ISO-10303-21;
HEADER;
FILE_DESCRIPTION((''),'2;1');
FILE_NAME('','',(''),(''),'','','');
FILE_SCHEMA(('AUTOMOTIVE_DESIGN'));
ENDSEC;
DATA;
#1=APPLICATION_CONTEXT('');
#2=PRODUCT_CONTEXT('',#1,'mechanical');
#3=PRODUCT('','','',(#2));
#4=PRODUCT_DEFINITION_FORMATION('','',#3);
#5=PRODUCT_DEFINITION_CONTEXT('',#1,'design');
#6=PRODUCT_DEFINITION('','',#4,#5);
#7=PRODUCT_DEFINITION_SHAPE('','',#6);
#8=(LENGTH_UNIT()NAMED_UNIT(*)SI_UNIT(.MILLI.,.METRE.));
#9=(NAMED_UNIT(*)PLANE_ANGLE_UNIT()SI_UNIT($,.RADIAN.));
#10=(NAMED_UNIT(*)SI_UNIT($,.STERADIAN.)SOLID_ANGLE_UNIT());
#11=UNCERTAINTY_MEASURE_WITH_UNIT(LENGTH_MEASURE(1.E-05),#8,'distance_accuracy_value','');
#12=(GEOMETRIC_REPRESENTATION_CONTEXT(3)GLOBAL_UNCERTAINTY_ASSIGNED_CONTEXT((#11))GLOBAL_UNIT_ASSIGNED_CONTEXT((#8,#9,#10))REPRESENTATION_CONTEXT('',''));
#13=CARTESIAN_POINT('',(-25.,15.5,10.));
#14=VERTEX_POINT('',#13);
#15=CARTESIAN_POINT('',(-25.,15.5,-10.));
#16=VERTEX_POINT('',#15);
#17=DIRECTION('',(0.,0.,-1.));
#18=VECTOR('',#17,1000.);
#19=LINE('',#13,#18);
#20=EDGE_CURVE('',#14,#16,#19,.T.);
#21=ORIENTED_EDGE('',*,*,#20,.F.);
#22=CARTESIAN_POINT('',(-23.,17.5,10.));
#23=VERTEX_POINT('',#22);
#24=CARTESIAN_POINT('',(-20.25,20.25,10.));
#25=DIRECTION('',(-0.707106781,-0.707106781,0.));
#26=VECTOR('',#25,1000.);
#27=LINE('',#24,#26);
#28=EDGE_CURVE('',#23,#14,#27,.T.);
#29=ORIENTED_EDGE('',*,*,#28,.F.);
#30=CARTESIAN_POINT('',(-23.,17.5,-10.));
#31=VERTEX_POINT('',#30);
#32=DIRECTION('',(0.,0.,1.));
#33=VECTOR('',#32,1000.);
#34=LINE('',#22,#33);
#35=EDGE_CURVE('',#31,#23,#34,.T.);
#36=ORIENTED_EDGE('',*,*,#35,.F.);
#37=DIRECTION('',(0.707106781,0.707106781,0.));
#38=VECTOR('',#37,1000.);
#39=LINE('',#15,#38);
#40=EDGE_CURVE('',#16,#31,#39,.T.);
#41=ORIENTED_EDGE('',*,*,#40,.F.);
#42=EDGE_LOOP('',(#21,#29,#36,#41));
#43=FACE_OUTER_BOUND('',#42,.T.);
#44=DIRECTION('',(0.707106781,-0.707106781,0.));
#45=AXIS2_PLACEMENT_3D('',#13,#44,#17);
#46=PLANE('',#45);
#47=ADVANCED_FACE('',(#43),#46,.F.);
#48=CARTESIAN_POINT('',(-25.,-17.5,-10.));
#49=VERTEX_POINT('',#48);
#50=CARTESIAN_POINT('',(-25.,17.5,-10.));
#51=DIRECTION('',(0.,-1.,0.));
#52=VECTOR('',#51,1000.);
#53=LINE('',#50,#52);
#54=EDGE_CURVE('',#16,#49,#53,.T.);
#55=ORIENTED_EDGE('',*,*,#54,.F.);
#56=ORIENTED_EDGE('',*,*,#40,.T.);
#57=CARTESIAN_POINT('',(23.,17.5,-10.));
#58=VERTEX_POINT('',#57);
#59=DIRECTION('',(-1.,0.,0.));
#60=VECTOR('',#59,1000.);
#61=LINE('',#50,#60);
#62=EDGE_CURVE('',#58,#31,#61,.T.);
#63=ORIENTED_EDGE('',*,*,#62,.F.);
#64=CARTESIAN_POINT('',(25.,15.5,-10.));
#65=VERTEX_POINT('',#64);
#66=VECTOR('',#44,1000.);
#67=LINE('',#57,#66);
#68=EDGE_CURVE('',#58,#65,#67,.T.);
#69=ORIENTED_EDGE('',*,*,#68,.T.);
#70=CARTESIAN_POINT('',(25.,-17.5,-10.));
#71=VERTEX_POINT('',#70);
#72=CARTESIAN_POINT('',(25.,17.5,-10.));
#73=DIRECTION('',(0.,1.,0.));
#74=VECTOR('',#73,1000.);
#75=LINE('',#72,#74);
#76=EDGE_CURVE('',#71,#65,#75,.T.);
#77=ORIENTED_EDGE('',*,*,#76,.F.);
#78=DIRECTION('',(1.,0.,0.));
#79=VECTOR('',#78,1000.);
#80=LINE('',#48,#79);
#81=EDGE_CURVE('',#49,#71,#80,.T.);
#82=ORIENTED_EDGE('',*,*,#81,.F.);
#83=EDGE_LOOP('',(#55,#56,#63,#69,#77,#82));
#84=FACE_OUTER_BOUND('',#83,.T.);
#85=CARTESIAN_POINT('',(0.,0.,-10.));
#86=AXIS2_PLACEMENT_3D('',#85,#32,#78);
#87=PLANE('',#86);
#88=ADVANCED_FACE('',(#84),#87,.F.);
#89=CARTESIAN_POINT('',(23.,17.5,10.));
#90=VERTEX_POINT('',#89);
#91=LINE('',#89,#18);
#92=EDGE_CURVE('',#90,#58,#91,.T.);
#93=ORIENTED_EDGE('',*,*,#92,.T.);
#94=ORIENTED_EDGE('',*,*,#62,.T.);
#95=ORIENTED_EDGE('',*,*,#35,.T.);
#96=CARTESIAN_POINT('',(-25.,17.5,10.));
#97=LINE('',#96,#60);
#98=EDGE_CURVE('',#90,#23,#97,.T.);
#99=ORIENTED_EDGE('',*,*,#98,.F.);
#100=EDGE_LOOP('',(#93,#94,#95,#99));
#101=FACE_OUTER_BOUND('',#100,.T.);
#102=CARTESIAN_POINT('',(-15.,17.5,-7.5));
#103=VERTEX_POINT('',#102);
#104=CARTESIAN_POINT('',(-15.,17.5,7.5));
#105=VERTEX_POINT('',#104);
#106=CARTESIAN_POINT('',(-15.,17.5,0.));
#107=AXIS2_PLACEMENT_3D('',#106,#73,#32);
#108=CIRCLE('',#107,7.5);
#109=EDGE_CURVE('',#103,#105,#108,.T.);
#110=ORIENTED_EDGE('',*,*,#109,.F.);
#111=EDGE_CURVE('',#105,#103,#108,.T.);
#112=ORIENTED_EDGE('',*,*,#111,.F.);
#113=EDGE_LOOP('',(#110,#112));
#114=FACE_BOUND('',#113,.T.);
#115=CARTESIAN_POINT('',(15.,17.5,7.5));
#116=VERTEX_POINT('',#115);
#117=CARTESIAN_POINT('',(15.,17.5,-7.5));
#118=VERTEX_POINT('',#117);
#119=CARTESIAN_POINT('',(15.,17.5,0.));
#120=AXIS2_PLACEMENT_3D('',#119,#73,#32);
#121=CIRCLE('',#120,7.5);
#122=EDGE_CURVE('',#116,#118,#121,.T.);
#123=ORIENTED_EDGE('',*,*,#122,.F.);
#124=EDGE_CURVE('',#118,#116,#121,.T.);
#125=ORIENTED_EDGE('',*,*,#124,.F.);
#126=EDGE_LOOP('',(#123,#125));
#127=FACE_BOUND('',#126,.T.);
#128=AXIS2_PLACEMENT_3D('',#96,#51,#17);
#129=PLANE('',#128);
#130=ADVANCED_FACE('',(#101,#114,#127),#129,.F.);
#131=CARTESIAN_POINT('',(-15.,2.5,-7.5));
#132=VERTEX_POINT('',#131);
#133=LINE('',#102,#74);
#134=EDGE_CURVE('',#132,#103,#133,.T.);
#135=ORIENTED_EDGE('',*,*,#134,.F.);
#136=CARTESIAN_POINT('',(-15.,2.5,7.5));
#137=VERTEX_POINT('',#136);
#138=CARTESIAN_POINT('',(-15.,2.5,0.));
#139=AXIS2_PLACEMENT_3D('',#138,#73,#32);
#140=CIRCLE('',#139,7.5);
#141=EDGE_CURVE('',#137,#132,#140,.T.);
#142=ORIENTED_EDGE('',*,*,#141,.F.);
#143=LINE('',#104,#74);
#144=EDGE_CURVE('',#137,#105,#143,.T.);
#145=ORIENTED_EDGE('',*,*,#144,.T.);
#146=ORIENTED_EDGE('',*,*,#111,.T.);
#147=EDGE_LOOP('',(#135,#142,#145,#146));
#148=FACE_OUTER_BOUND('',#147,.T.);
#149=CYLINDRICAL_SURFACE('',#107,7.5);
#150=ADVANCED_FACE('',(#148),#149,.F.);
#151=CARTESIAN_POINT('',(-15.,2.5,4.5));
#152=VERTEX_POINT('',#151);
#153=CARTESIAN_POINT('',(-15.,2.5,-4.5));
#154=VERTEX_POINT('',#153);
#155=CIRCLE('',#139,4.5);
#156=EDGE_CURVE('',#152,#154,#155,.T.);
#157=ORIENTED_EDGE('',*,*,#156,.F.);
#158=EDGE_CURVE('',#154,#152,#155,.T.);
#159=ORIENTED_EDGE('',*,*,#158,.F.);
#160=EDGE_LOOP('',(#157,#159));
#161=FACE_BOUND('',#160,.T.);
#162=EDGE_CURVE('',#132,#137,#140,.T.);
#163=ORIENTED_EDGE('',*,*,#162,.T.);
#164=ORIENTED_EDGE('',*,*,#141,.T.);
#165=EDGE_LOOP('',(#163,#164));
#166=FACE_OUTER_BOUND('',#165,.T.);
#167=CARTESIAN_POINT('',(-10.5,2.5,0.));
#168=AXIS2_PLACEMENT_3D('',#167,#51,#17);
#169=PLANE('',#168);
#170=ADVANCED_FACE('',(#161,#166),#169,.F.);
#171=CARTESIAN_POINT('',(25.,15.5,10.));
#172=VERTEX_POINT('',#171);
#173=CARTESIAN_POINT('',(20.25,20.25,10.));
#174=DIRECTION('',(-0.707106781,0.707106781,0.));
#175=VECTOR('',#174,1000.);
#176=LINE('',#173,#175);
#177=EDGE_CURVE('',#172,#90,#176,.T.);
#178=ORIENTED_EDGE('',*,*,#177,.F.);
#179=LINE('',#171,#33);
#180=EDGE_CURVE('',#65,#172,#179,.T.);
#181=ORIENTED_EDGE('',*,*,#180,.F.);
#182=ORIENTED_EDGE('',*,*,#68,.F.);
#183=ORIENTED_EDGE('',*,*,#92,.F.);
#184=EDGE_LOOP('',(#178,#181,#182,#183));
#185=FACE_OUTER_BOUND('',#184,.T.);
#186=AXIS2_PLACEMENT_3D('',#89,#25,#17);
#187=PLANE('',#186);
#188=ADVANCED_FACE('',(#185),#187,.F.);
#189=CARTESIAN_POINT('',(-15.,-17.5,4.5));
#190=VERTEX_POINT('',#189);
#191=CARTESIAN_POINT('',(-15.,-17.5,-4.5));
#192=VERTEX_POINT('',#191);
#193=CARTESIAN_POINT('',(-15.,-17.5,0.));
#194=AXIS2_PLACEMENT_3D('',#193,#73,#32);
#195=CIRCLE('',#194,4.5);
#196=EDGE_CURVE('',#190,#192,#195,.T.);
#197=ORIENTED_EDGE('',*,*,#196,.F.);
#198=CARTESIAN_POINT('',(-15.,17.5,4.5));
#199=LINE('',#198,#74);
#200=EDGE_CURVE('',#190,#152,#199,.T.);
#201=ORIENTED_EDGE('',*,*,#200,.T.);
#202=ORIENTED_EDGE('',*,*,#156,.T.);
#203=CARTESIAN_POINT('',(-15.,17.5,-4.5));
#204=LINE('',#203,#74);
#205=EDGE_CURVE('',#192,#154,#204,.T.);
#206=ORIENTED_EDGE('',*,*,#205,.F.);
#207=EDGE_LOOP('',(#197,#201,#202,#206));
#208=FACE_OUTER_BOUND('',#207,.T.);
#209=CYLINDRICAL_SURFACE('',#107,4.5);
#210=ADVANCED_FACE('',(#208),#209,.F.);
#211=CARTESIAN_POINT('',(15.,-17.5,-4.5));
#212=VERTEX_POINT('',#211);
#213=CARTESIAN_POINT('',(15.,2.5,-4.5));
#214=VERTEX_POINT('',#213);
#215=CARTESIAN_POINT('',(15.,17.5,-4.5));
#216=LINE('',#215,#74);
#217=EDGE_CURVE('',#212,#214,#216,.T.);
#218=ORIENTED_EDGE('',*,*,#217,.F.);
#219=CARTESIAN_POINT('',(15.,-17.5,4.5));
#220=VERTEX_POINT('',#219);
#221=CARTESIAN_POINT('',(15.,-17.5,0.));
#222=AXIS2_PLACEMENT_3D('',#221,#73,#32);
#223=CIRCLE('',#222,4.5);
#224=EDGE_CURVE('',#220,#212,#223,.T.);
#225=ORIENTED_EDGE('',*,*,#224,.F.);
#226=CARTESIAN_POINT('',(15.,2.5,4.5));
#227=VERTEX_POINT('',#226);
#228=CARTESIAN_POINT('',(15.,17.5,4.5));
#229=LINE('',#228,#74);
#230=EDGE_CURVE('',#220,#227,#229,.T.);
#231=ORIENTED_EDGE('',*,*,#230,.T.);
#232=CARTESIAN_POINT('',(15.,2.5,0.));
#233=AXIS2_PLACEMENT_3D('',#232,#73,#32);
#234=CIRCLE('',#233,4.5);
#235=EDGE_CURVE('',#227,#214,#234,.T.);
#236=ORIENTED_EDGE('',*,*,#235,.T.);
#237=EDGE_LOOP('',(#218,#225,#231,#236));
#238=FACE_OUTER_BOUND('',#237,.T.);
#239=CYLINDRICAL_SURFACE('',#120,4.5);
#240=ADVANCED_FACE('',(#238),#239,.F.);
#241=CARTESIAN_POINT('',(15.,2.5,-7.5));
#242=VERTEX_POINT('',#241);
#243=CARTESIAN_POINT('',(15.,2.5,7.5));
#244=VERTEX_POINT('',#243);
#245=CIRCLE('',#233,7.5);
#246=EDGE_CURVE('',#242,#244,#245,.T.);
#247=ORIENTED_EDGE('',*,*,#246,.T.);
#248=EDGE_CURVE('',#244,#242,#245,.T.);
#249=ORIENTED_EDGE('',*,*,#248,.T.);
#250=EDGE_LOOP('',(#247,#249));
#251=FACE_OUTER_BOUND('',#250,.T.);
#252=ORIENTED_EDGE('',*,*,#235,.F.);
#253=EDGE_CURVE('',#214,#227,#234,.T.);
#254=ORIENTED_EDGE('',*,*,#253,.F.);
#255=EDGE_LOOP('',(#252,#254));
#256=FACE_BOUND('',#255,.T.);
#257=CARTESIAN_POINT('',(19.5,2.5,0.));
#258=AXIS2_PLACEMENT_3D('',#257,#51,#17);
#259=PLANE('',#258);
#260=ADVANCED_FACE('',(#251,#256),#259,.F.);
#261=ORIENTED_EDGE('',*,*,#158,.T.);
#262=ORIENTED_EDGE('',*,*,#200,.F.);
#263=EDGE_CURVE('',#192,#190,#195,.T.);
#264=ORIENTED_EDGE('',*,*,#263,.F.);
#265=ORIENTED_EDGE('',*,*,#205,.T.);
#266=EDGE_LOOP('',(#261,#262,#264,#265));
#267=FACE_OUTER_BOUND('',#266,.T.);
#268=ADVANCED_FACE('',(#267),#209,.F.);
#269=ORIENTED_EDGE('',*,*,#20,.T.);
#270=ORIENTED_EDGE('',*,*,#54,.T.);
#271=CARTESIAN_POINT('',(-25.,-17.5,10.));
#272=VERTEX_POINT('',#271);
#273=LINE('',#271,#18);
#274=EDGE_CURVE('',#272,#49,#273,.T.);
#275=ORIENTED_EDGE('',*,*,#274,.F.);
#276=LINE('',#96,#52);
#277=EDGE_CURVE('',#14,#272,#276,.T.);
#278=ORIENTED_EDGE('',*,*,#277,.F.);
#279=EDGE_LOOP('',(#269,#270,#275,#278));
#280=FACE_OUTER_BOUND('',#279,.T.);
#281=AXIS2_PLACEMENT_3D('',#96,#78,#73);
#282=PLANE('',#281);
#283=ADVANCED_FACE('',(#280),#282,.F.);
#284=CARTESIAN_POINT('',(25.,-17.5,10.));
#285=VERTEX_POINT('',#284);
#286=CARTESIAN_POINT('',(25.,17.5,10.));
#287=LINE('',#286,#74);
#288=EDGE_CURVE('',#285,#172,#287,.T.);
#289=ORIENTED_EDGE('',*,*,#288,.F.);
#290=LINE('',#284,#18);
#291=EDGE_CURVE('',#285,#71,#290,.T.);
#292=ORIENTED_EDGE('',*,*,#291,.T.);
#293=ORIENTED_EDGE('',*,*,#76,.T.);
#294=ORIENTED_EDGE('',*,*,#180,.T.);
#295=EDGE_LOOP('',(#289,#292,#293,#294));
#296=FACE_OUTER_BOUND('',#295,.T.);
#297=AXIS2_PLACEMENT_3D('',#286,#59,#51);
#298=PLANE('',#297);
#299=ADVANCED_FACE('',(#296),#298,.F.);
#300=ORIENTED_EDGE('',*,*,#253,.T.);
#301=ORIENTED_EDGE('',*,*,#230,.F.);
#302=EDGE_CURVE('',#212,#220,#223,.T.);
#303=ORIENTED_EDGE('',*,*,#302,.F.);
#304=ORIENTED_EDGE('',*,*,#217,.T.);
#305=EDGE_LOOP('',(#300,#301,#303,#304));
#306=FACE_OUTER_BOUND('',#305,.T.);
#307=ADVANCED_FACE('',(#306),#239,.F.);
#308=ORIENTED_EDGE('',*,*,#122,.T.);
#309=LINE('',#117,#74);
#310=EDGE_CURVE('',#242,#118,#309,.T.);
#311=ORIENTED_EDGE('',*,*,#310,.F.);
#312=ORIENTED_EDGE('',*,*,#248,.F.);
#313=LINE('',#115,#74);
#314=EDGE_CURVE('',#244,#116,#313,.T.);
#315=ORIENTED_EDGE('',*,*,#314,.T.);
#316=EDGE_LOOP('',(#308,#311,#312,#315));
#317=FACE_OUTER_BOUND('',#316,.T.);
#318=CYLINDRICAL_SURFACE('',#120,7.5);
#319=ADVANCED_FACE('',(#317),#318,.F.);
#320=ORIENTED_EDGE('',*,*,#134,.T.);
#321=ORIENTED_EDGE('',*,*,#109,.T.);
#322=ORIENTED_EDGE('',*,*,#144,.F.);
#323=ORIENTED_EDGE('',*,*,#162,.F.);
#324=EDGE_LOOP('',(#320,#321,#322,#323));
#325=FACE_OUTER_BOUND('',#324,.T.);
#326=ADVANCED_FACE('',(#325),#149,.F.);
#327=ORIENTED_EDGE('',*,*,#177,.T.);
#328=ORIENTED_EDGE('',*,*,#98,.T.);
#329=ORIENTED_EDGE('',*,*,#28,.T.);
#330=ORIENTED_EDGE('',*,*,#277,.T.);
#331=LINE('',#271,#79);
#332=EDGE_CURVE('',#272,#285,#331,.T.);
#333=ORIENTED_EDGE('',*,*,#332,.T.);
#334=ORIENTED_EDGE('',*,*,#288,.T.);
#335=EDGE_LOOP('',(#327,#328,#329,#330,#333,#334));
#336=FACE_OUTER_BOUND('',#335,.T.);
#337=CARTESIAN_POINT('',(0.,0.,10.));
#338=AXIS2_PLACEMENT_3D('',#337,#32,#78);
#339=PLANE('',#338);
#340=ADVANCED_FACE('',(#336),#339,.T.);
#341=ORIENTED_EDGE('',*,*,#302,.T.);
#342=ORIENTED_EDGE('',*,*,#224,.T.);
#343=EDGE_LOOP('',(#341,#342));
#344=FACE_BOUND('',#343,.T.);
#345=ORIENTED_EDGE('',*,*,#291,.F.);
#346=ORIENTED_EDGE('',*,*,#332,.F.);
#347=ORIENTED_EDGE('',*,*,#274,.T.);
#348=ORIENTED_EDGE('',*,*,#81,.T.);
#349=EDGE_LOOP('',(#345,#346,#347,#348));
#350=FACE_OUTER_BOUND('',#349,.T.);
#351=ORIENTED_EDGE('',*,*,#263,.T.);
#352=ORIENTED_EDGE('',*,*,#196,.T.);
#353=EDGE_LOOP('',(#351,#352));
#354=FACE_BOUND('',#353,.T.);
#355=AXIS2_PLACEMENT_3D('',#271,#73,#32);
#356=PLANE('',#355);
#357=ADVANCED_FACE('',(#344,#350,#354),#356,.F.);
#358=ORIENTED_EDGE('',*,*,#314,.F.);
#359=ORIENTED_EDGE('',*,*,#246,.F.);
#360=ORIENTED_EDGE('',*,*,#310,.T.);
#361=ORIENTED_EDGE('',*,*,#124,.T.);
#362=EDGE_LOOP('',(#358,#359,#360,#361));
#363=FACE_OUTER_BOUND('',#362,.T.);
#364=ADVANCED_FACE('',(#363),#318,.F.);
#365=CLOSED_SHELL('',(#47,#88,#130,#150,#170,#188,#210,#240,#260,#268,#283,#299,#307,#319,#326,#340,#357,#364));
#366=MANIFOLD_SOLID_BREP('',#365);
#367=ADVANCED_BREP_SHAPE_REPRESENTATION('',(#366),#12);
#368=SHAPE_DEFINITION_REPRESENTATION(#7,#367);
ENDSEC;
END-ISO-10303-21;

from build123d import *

# Parameters (mm, degrees)
SKETCH_2_W                   = 50
SKETCH_2_H                   = 35
EXTRUDE_1_DEPTH              = 10
HOLE_WIZARD_M8_1_D           = 9
HOLE_WIZARD_M8_1_CBORE_D     = 15
HOLE_WIZARD_M8_1_CBORE_DEPTH = 15
CHAMFER_1_SIZE               = 2


with BuildPart() as part:
    # 草图2 → 凸台-拉伸1 (new, symmetric)
    with BuildSketch(Plane.XY):
        Rectangle(SKETCH_2_W, SKETCH_2_H)
    extrude(amount=EXTRUDE_1_DEPTH, both=True)

    # M8 六角凹头螺钉的柱形沉头孔1 (through all)
    with Locations(Plane(origin=(0, 17.5, 0), x_dir=(1, 0, 0), z_dir=(0, 1, 0))):
        with Locations((15, 0), (-15, 0)):
            CounterBoreHole(HOLE_WIZARD_M8_1_D / 2, HOLE_WIZARD_M8_1_CBORE_D / 2, HOLE_WIZARD_M8_1_CBORE_DEPTH)

    # 倒角1
    chamfer_1_edges = [part.edges().sort_by_distance(p)[0] for p in [
        (-25, 17.5, 0),
        (25, 17.5, 0),
    ]]
    chamfer(chamfer_1_edges, length=CHAMFER_1_SIZE)


solid = part.part
